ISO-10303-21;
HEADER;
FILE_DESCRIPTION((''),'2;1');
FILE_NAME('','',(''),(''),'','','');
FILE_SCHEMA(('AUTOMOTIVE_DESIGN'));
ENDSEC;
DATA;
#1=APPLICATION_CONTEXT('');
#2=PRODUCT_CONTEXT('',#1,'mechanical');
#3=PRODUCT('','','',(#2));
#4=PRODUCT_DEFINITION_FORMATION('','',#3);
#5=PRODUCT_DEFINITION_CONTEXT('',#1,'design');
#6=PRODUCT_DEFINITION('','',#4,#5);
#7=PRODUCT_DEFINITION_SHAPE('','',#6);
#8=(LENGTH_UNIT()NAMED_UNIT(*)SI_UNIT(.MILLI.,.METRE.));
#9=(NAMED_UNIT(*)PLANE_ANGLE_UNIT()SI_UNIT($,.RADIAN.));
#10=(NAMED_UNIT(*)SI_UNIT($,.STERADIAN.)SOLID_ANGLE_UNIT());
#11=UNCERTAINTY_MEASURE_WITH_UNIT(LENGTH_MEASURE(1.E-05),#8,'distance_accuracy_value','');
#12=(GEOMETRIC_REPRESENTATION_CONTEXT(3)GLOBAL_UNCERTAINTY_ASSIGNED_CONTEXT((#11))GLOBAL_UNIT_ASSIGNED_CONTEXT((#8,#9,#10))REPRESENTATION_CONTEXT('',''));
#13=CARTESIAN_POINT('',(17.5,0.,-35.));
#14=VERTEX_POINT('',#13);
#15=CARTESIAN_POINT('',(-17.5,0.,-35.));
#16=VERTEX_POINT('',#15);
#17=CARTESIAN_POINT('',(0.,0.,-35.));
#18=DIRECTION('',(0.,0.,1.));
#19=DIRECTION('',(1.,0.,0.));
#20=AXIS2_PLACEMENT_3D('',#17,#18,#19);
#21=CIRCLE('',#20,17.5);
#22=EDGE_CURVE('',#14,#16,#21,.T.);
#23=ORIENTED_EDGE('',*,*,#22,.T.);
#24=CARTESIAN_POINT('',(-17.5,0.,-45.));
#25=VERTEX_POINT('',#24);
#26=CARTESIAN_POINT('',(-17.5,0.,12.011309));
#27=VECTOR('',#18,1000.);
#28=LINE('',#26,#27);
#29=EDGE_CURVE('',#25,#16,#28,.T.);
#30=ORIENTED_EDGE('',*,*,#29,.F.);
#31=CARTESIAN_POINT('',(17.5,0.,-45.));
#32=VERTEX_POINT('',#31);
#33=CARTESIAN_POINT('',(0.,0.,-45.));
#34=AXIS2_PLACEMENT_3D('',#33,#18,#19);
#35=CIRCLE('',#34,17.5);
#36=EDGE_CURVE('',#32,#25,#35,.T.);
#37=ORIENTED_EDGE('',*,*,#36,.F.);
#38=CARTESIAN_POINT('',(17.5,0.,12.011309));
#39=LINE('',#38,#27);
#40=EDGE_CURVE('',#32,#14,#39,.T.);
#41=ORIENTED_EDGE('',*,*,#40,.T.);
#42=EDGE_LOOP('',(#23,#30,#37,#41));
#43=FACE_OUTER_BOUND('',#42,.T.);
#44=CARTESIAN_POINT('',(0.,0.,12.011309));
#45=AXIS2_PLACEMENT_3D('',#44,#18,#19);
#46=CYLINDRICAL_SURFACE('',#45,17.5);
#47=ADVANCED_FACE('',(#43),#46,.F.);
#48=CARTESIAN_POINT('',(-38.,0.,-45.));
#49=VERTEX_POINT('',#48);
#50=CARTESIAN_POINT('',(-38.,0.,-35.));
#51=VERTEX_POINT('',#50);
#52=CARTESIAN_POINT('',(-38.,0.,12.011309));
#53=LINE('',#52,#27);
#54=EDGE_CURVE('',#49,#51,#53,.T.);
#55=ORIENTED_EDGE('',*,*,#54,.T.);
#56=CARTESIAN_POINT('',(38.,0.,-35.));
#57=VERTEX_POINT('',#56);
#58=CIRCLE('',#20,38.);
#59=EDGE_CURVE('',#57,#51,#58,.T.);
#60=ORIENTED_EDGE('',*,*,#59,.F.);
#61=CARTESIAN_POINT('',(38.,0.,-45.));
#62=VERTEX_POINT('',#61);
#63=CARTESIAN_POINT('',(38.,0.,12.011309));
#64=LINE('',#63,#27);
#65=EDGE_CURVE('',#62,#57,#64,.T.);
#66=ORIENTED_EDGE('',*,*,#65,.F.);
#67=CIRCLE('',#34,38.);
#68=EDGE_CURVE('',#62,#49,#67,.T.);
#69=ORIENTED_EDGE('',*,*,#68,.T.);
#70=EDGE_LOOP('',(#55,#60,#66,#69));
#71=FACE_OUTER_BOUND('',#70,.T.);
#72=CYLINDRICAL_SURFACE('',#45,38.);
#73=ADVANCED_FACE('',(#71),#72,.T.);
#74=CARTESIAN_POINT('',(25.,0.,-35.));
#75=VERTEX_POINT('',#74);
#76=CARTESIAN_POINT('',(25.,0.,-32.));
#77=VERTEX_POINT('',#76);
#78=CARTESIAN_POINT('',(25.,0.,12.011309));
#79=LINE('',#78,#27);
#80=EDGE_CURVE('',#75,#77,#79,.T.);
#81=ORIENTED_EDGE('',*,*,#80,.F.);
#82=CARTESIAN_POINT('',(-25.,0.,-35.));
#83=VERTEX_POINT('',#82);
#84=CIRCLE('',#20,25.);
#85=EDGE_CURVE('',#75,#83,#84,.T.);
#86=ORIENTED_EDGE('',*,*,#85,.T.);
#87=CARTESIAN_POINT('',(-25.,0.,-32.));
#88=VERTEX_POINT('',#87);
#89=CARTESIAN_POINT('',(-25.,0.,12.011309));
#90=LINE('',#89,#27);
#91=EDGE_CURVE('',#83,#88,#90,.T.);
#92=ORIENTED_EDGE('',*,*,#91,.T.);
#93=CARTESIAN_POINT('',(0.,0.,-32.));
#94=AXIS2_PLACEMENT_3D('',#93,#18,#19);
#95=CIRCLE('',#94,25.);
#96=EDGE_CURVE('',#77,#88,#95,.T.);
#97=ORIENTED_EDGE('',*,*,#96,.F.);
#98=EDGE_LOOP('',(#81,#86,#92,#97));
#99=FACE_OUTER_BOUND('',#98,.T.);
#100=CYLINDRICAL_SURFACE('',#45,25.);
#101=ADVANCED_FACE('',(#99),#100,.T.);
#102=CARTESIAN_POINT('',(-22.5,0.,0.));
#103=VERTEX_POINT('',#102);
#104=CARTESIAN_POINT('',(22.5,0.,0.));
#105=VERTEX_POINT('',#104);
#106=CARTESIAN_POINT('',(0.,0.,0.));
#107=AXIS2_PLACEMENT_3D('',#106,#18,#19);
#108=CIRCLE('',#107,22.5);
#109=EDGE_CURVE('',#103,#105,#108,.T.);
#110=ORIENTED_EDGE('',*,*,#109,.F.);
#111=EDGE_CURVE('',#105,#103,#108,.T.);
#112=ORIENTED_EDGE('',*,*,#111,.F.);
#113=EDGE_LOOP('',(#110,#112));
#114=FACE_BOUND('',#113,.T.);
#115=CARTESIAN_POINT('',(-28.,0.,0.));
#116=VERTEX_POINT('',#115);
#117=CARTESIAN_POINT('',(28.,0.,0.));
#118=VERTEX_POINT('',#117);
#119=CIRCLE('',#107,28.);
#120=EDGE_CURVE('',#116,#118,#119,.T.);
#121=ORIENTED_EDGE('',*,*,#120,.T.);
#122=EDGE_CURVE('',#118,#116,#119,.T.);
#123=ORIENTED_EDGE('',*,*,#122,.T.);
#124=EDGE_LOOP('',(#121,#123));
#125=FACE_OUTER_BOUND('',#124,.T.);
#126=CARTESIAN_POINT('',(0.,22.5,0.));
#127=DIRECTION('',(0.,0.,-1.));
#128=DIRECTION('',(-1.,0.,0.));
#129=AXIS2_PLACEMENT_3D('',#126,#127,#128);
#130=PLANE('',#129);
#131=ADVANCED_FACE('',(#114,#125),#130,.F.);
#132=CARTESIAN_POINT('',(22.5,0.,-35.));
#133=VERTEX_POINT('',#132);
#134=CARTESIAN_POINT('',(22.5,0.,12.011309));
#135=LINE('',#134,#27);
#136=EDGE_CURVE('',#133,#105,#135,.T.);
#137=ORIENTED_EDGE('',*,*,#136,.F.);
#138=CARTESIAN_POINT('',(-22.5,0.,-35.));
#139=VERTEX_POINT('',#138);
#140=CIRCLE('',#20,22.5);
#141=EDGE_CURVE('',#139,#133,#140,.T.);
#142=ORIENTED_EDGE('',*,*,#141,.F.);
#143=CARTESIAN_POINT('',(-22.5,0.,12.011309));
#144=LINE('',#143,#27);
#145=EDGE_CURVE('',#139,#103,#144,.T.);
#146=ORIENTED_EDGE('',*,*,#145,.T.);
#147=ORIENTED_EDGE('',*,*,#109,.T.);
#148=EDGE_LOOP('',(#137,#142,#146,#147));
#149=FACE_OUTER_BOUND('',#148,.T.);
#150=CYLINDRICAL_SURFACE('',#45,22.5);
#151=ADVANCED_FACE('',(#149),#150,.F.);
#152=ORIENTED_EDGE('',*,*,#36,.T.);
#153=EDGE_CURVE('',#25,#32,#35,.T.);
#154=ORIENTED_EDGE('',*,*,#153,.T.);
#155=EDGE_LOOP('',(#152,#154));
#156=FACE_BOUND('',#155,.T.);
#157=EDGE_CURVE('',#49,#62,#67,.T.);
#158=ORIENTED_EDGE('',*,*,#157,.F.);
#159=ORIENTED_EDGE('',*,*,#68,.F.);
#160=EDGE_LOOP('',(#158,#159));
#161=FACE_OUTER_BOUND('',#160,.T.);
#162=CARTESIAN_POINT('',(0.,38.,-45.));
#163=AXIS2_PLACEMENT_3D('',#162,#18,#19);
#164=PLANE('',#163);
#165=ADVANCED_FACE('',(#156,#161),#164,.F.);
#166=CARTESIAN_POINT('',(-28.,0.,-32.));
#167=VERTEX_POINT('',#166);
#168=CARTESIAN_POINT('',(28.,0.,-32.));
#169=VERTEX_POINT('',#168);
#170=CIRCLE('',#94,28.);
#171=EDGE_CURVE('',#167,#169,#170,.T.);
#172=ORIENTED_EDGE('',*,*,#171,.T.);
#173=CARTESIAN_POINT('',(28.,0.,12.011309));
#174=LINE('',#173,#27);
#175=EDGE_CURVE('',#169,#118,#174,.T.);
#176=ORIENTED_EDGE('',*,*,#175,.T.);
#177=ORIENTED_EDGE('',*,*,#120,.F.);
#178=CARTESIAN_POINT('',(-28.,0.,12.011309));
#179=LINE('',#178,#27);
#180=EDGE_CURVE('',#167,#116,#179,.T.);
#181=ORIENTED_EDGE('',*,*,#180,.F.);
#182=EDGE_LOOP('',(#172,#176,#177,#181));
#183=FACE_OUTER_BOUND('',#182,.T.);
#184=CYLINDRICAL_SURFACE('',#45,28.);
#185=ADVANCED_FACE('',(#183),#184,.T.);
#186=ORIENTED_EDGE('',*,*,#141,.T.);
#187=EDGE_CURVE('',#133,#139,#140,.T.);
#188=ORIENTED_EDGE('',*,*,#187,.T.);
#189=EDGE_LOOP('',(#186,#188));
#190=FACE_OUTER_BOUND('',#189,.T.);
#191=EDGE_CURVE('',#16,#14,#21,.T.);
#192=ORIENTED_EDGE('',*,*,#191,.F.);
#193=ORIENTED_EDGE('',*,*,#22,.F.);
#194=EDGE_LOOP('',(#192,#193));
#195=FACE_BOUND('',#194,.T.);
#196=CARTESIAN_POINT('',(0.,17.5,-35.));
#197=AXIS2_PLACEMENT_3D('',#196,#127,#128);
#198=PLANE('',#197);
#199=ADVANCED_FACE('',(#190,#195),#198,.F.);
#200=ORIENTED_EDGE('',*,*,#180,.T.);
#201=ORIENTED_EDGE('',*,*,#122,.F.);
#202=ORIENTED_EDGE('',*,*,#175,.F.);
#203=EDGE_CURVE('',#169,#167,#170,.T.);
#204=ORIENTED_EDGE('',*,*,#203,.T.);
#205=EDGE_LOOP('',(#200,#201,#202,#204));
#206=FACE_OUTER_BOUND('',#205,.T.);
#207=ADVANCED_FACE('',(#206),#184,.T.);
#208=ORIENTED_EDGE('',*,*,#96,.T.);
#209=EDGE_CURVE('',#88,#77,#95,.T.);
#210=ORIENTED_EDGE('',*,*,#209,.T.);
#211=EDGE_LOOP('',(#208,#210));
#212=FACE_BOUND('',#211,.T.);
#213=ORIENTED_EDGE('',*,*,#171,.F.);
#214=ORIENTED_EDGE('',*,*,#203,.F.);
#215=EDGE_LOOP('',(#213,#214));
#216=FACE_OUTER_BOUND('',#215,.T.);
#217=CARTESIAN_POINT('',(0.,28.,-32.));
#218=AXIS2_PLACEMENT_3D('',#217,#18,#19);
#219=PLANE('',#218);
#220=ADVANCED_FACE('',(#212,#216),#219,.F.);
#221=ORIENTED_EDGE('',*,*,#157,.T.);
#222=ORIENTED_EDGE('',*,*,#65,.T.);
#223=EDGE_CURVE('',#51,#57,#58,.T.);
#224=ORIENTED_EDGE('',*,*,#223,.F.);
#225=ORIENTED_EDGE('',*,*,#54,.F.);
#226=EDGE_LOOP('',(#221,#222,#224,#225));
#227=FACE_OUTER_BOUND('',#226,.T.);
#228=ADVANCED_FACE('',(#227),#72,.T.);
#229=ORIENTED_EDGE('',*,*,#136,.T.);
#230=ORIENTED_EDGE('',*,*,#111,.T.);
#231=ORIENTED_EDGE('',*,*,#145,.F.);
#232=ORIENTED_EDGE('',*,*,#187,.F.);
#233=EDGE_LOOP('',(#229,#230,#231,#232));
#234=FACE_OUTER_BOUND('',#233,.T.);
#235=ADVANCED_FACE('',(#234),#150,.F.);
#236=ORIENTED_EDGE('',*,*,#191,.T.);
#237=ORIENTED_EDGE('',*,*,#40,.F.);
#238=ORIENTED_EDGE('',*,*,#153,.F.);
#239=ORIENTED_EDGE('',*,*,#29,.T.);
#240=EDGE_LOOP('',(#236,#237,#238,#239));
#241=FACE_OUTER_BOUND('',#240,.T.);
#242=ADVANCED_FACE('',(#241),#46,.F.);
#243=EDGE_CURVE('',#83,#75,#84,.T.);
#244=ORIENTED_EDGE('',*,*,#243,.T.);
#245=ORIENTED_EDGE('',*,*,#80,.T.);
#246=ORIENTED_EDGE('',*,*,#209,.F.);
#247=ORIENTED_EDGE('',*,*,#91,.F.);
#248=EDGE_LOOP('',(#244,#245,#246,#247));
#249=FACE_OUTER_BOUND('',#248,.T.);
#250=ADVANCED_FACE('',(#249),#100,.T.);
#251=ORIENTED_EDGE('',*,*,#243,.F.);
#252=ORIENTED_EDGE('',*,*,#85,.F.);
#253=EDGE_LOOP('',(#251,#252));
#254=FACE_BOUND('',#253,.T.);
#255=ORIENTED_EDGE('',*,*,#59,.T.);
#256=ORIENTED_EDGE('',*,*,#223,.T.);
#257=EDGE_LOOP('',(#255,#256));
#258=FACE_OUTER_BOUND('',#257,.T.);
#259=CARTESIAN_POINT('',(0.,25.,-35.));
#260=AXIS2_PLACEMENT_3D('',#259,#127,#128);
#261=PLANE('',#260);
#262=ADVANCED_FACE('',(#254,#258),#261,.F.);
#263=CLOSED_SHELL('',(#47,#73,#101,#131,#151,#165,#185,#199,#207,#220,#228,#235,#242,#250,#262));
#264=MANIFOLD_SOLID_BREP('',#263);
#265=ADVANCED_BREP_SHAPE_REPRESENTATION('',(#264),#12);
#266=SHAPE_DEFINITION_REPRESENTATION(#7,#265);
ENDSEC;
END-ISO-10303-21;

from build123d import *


with BuildPart() as part:
    # Sketch1 → Revolve1 (revolve)
    with BuildSketch(Plane(origin=(0, 0, 0), x_dir=(0, 0, -1), z_dir=(1, 0, 0)), mode=Mode.PRIVATE) as revolve1_sk:
        Polygon((0, 22.5), (0, 28), (32, 28), (32, 25), (35, 25), (35, 38), (45, 38), (45, 17.5), (35, 17.5), (35, 22.5), align=None)
    revolve(revolve1_sk.sketch.rotate(Axis((0, 0, 12.011308803), (0, 0, -1)), 90), axis=Axis((0, 0, 12.011308803), (0, 0, -1)))


solid = part.part
